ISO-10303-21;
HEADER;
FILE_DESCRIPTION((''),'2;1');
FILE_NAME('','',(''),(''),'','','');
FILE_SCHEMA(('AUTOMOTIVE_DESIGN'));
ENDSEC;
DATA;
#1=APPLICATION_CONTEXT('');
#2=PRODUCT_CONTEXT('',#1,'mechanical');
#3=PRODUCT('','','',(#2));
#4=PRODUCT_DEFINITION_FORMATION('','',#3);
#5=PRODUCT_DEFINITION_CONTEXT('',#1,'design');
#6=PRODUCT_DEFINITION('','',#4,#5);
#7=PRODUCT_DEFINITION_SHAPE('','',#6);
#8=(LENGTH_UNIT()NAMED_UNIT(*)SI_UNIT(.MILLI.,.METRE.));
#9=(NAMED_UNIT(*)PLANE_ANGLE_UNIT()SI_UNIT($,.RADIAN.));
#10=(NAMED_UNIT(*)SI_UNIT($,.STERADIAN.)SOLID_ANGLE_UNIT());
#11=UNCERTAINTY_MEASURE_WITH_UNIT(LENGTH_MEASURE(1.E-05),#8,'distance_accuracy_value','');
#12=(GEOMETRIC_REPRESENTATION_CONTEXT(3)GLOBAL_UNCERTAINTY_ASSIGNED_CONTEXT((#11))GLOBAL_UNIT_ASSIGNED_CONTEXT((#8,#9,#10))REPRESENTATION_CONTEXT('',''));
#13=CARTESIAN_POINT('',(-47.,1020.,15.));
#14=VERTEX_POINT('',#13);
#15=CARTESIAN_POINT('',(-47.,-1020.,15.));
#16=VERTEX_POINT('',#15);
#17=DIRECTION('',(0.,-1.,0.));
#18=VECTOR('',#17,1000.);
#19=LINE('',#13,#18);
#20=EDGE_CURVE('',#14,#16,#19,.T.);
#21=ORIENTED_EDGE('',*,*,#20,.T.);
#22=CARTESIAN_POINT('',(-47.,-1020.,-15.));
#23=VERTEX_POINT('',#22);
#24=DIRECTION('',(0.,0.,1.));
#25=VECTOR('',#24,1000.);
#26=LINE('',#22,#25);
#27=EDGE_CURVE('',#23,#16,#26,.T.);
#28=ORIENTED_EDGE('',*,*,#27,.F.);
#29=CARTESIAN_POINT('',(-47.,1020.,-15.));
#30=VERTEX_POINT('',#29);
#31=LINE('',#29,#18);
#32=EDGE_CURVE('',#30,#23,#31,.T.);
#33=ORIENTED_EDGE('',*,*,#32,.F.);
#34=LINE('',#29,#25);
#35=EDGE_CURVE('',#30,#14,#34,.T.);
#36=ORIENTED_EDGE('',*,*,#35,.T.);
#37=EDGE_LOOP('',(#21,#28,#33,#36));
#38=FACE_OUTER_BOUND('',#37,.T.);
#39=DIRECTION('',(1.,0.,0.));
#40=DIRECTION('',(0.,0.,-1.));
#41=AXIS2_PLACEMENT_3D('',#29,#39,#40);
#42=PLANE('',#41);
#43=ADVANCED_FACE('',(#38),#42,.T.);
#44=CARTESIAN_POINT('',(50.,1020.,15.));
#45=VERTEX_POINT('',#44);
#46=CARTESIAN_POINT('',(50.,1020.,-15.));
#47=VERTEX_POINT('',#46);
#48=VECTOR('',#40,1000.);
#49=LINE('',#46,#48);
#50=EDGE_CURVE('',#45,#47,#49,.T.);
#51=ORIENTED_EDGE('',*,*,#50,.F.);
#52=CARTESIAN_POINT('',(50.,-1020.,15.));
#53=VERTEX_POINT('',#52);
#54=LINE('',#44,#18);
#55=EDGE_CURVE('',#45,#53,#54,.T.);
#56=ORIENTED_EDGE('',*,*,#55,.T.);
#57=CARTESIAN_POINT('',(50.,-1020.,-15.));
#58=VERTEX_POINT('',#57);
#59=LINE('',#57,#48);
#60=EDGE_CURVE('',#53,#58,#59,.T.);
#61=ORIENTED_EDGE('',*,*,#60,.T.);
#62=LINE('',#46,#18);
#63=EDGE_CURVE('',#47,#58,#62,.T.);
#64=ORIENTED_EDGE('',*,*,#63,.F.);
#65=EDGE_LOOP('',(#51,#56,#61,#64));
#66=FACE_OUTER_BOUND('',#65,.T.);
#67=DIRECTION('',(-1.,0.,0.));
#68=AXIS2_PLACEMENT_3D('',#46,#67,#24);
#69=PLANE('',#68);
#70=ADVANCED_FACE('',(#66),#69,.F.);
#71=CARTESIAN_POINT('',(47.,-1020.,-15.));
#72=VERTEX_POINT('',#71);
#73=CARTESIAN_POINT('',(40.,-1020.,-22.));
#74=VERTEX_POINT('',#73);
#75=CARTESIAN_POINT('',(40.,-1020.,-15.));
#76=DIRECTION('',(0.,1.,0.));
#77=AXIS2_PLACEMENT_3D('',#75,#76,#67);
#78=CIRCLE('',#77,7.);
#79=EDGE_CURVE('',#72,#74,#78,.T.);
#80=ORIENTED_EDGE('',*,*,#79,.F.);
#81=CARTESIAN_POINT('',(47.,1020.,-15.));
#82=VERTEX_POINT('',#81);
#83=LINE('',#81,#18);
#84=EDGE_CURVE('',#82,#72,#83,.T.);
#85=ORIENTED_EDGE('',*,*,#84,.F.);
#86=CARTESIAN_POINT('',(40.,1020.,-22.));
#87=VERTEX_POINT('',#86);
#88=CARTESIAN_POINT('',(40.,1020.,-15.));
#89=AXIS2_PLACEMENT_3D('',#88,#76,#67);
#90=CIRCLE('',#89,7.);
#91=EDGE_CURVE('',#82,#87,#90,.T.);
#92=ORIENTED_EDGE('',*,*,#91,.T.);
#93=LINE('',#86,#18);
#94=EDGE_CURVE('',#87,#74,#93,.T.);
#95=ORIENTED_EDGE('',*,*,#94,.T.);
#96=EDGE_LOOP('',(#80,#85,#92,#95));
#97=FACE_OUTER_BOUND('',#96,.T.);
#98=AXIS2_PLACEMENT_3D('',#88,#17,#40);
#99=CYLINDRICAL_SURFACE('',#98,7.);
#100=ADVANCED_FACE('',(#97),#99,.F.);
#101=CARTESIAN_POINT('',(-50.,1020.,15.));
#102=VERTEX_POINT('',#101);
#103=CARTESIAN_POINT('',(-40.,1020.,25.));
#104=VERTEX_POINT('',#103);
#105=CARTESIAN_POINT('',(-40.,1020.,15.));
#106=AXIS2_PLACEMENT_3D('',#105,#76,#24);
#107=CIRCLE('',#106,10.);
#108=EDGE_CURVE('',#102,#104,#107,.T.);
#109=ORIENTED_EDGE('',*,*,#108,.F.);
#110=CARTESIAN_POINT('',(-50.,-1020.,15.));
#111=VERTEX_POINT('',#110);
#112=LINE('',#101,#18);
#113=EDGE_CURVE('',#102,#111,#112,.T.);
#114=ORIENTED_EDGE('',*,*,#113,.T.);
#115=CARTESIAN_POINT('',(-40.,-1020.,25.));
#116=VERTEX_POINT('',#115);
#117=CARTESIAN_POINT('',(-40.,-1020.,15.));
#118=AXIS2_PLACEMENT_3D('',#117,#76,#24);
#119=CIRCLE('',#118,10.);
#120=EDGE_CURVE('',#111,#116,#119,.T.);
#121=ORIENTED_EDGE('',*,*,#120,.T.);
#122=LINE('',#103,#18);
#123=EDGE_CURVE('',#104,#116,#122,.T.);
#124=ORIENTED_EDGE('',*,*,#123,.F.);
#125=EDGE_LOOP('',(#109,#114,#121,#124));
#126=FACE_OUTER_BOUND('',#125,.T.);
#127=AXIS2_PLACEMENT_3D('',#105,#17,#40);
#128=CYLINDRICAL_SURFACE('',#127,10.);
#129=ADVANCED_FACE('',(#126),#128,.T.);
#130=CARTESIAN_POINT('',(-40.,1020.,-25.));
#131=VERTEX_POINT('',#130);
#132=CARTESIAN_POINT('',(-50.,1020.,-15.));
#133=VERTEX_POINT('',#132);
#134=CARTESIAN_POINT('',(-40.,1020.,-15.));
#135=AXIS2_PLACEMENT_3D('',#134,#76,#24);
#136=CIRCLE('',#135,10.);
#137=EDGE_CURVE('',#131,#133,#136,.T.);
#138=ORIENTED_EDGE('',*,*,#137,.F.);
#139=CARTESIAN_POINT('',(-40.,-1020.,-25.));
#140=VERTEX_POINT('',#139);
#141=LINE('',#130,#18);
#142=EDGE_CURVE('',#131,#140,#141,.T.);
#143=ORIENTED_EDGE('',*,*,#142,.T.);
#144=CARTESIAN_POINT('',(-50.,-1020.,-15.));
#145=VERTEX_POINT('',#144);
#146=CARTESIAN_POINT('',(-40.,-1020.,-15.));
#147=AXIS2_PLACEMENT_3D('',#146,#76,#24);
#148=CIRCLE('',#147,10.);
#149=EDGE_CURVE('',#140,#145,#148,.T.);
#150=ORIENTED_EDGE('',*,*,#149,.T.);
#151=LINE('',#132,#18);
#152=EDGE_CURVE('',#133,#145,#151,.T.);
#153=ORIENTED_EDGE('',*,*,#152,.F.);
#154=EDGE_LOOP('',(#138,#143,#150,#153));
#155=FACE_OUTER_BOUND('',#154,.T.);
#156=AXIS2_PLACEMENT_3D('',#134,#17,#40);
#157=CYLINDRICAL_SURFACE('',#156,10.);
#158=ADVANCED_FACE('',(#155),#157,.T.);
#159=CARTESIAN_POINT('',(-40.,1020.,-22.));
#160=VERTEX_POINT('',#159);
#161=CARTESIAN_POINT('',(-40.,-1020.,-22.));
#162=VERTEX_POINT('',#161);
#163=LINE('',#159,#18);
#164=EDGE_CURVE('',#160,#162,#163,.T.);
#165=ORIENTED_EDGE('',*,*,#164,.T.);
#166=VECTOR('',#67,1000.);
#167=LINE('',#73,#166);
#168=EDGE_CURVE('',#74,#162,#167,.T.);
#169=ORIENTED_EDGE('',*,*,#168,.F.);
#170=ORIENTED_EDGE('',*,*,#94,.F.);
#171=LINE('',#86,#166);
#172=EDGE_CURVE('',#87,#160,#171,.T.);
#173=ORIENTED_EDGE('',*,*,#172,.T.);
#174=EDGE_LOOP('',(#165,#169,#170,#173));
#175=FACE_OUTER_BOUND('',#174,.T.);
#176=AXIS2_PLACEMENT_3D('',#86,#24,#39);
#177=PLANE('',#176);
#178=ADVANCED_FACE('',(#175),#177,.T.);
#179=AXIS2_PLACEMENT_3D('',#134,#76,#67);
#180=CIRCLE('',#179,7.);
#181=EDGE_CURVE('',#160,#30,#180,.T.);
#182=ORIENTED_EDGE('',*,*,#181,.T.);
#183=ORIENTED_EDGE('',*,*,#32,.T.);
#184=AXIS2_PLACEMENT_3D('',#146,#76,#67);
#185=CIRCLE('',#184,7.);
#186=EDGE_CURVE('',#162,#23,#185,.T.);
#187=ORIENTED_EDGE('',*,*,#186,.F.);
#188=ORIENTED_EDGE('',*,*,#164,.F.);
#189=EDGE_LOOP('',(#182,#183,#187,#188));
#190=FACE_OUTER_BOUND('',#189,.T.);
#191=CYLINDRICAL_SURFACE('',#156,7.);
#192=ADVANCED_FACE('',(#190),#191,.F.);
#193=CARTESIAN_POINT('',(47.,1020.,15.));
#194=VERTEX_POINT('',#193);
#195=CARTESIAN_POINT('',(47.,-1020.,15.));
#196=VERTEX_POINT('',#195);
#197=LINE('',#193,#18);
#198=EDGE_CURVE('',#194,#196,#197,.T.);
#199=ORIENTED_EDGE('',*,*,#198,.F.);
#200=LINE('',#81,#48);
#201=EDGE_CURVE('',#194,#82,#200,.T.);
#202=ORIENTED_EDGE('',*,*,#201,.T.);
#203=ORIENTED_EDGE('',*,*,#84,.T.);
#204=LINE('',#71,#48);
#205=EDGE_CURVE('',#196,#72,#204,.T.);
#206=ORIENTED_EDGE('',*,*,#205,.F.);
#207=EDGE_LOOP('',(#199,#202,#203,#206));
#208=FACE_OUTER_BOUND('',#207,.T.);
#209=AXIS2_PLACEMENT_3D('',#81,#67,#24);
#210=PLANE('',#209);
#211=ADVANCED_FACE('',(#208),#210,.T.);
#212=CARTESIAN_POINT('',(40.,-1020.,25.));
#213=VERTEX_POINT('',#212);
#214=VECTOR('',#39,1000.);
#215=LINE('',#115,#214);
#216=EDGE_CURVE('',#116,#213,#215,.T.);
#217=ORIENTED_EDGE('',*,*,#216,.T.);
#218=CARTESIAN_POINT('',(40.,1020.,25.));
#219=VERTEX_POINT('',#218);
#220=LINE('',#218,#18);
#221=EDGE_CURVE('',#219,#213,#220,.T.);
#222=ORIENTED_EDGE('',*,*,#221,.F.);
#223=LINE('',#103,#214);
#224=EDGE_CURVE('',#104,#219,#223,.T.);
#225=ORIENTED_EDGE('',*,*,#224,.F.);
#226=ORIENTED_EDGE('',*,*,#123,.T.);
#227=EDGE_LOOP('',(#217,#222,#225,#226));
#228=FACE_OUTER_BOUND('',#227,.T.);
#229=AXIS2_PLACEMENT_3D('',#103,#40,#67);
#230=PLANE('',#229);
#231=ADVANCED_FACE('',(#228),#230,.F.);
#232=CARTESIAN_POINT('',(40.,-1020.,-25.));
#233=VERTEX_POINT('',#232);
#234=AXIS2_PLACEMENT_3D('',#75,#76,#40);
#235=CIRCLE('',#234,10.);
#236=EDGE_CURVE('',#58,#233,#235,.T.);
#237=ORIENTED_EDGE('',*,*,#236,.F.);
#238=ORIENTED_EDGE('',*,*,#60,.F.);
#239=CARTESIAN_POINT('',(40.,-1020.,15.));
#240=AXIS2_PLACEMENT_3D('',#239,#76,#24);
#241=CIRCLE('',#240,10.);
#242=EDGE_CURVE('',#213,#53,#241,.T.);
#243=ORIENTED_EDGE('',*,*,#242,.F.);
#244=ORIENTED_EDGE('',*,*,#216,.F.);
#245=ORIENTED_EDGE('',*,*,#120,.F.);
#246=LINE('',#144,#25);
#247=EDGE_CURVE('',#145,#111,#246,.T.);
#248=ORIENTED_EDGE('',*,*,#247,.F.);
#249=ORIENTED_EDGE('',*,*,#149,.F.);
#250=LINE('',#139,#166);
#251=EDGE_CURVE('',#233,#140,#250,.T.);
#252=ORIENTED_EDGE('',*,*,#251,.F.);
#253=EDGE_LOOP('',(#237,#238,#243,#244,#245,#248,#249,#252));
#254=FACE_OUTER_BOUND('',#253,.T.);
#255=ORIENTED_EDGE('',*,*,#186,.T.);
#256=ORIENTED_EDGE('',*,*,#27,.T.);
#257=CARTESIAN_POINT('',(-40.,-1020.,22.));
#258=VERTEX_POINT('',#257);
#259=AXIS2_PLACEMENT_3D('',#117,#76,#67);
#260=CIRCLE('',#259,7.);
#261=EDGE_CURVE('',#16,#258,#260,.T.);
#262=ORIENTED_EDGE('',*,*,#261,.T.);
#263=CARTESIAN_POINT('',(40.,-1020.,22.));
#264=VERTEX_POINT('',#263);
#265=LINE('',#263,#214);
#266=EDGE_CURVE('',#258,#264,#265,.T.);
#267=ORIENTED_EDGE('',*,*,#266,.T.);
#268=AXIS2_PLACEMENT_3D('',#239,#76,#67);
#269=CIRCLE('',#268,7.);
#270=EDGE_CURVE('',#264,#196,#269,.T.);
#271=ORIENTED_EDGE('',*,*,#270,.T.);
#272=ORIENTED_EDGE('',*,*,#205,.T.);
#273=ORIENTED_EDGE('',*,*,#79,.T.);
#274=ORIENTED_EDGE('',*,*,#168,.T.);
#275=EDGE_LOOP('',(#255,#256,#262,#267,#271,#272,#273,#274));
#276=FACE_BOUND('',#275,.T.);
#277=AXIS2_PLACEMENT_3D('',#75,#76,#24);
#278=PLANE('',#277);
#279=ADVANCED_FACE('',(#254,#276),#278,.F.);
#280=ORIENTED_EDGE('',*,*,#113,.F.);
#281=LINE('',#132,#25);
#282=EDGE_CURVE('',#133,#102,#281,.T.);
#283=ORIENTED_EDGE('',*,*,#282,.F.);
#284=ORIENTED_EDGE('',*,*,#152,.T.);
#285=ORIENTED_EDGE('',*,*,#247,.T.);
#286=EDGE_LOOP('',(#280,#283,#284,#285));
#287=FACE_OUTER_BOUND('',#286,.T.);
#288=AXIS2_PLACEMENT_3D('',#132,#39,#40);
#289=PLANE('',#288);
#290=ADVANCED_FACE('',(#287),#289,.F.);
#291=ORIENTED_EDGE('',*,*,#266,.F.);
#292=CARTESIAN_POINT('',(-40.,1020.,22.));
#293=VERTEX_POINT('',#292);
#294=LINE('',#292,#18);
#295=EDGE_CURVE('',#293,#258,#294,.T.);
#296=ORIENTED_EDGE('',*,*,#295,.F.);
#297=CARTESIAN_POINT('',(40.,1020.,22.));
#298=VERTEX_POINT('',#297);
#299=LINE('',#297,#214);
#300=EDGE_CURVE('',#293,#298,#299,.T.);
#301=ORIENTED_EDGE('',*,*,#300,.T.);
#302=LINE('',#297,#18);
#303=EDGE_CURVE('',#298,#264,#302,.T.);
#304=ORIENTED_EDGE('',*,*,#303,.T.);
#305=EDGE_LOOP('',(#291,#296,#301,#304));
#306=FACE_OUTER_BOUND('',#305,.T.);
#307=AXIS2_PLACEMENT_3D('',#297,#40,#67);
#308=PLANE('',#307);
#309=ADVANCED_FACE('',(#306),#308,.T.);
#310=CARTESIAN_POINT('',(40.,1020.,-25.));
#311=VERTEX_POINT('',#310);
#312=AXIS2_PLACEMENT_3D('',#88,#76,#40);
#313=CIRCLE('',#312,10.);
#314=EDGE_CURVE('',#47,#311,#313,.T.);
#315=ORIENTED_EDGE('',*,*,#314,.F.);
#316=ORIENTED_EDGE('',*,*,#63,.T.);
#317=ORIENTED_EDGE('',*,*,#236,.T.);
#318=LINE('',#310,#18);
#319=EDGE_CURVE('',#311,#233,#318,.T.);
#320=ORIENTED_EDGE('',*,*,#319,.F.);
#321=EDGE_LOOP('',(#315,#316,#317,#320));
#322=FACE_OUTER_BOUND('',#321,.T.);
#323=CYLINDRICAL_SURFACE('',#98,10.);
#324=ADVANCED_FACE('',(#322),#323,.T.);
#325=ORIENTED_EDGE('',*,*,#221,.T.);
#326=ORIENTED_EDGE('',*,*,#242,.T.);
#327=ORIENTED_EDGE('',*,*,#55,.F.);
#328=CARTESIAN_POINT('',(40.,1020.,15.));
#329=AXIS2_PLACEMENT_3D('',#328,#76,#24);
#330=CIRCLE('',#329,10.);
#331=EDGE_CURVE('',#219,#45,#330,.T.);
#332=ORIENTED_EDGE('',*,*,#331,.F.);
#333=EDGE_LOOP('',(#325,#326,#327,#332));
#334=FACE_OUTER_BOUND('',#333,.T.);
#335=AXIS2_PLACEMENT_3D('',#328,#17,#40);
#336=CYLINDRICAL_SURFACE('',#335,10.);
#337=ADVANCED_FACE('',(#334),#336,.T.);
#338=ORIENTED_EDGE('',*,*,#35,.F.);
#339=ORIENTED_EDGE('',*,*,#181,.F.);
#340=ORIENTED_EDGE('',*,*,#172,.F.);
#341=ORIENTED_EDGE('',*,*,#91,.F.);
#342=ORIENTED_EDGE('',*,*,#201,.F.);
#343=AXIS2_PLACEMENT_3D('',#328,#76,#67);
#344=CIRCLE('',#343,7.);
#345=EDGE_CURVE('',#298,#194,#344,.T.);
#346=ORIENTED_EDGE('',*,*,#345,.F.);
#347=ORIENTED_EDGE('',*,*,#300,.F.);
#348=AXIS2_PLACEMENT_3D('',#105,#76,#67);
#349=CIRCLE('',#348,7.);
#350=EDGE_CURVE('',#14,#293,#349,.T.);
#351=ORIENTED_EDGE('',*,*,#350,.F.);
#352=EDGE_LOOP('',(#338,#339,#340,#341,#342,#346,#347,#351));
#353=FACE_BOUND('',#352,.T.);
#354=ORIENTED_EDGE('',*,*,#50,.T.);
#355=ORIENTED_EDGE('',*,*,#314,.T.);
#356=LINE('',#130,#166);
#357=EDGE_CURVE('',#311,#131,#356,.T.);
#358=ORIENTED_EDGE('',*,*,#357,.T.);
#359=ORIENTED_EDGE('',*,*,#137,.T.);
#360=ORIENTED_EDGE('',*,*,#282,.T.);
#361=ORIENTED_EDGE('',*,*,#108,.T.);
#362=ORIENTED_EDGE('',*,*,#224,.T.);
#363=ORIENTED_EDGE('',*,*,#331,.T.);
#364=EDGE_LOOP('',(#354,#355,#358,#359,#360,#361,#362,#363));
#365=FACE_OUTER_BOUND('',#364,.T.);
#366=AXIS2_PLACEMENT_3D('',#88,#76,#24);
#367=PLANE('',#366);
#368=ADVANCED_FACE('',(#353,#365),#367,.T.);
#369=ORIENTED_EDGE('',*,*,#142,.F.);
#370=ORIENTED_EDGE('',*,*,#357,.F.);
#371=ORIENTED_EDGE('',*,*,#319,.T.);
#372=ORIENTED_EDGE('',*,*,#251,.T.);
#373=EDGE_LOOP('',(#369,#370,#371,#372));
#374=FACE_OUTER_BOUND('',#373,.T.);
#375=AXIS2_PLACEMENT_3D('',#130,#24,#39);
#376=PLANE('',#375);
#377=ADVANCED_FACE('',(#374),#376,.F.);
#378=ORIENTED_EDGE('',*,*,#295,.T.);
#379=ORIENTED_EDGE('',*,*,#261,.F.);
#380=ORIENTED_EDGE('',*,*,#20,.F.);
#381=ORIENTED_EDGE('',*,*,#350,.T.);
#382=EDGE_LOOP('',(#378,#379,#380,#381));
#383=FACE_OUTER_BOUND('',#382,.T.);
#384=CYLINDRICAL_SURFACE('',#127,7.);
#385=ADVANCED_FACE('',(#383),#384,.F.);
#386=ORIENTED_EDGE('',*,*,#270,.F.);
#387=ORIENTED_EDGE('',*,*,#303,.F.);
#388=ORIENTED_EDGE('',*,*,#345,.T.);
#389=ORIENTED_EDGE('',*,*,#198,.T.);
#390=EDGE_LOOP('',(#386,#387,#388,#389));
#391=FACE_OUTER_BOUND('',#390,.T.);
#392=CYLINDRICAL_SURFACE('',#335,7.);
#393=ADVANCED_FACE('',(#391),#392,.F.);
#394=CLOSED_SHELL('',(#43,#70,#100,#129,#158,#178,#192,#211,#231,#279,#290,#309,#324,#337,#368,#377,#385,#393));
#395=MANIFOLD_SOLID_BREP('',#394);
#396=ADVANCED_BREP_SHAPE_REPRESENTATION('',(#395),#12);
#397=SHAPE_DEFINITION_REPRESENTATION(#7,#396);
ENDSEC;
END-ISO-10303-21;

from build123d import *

# Parameters (mm, degrees)
EXTRUDE_THIN1_DEPTH = 1020


with BuildPart() as part:
    # Sketch1 → Extrude-Thin1 (new, symmetric)
    with BuildSketch(Plane(origin=(0, 0, 0), x_dir=(1, 0, 0), z_dir=(0, 1, 0))):
        with BuildLine():
            Line((-40, 25), (40, 25))
            ThreePointArc((40, 25), (47.071067812, 22.071067812), (50, 15))
            Line((50, 15), (50, -15))
            ThreePointArc((50, -15), (47.071067812, -22.071067812), (40, -25))
            Line((40, -25), (-40, -25))
            ThreePointArc((-40, -25), (-47.071067812, -22.071067812), (-50, -15))
            Line((-50, -15), (-50, 15))
            ThreePointArc((-50, 15), (-47.071067812, 22.071067812), (-40, 25))
        make_face()
        with BuildLine():
            Line((-40, 22), (40, 22))
            ThreePointArc((40, 22), (44.949747468, 19.949747468), (47, 15))
            Line((47, 15), (47, -15))
            ThreePointArc((47, -15), (44.949747468, -19.949747468), (40, -22))
            Line((40, -22), (-40, -22))
            ThreePointArc((-40, -22), (-44.949747468, -19.949747468), (-47, -15))
            Line((-47, -15), (-47, 15))
            ThreePointArc((-47, 15), (-44.949747468, 19.949747468), (-40, 22))
        make_face(mode=Mode.SUBTRACT)
    extrude(amount=EXTRUDE_THIN1_DEPTH, both=True)


solid = part.part
